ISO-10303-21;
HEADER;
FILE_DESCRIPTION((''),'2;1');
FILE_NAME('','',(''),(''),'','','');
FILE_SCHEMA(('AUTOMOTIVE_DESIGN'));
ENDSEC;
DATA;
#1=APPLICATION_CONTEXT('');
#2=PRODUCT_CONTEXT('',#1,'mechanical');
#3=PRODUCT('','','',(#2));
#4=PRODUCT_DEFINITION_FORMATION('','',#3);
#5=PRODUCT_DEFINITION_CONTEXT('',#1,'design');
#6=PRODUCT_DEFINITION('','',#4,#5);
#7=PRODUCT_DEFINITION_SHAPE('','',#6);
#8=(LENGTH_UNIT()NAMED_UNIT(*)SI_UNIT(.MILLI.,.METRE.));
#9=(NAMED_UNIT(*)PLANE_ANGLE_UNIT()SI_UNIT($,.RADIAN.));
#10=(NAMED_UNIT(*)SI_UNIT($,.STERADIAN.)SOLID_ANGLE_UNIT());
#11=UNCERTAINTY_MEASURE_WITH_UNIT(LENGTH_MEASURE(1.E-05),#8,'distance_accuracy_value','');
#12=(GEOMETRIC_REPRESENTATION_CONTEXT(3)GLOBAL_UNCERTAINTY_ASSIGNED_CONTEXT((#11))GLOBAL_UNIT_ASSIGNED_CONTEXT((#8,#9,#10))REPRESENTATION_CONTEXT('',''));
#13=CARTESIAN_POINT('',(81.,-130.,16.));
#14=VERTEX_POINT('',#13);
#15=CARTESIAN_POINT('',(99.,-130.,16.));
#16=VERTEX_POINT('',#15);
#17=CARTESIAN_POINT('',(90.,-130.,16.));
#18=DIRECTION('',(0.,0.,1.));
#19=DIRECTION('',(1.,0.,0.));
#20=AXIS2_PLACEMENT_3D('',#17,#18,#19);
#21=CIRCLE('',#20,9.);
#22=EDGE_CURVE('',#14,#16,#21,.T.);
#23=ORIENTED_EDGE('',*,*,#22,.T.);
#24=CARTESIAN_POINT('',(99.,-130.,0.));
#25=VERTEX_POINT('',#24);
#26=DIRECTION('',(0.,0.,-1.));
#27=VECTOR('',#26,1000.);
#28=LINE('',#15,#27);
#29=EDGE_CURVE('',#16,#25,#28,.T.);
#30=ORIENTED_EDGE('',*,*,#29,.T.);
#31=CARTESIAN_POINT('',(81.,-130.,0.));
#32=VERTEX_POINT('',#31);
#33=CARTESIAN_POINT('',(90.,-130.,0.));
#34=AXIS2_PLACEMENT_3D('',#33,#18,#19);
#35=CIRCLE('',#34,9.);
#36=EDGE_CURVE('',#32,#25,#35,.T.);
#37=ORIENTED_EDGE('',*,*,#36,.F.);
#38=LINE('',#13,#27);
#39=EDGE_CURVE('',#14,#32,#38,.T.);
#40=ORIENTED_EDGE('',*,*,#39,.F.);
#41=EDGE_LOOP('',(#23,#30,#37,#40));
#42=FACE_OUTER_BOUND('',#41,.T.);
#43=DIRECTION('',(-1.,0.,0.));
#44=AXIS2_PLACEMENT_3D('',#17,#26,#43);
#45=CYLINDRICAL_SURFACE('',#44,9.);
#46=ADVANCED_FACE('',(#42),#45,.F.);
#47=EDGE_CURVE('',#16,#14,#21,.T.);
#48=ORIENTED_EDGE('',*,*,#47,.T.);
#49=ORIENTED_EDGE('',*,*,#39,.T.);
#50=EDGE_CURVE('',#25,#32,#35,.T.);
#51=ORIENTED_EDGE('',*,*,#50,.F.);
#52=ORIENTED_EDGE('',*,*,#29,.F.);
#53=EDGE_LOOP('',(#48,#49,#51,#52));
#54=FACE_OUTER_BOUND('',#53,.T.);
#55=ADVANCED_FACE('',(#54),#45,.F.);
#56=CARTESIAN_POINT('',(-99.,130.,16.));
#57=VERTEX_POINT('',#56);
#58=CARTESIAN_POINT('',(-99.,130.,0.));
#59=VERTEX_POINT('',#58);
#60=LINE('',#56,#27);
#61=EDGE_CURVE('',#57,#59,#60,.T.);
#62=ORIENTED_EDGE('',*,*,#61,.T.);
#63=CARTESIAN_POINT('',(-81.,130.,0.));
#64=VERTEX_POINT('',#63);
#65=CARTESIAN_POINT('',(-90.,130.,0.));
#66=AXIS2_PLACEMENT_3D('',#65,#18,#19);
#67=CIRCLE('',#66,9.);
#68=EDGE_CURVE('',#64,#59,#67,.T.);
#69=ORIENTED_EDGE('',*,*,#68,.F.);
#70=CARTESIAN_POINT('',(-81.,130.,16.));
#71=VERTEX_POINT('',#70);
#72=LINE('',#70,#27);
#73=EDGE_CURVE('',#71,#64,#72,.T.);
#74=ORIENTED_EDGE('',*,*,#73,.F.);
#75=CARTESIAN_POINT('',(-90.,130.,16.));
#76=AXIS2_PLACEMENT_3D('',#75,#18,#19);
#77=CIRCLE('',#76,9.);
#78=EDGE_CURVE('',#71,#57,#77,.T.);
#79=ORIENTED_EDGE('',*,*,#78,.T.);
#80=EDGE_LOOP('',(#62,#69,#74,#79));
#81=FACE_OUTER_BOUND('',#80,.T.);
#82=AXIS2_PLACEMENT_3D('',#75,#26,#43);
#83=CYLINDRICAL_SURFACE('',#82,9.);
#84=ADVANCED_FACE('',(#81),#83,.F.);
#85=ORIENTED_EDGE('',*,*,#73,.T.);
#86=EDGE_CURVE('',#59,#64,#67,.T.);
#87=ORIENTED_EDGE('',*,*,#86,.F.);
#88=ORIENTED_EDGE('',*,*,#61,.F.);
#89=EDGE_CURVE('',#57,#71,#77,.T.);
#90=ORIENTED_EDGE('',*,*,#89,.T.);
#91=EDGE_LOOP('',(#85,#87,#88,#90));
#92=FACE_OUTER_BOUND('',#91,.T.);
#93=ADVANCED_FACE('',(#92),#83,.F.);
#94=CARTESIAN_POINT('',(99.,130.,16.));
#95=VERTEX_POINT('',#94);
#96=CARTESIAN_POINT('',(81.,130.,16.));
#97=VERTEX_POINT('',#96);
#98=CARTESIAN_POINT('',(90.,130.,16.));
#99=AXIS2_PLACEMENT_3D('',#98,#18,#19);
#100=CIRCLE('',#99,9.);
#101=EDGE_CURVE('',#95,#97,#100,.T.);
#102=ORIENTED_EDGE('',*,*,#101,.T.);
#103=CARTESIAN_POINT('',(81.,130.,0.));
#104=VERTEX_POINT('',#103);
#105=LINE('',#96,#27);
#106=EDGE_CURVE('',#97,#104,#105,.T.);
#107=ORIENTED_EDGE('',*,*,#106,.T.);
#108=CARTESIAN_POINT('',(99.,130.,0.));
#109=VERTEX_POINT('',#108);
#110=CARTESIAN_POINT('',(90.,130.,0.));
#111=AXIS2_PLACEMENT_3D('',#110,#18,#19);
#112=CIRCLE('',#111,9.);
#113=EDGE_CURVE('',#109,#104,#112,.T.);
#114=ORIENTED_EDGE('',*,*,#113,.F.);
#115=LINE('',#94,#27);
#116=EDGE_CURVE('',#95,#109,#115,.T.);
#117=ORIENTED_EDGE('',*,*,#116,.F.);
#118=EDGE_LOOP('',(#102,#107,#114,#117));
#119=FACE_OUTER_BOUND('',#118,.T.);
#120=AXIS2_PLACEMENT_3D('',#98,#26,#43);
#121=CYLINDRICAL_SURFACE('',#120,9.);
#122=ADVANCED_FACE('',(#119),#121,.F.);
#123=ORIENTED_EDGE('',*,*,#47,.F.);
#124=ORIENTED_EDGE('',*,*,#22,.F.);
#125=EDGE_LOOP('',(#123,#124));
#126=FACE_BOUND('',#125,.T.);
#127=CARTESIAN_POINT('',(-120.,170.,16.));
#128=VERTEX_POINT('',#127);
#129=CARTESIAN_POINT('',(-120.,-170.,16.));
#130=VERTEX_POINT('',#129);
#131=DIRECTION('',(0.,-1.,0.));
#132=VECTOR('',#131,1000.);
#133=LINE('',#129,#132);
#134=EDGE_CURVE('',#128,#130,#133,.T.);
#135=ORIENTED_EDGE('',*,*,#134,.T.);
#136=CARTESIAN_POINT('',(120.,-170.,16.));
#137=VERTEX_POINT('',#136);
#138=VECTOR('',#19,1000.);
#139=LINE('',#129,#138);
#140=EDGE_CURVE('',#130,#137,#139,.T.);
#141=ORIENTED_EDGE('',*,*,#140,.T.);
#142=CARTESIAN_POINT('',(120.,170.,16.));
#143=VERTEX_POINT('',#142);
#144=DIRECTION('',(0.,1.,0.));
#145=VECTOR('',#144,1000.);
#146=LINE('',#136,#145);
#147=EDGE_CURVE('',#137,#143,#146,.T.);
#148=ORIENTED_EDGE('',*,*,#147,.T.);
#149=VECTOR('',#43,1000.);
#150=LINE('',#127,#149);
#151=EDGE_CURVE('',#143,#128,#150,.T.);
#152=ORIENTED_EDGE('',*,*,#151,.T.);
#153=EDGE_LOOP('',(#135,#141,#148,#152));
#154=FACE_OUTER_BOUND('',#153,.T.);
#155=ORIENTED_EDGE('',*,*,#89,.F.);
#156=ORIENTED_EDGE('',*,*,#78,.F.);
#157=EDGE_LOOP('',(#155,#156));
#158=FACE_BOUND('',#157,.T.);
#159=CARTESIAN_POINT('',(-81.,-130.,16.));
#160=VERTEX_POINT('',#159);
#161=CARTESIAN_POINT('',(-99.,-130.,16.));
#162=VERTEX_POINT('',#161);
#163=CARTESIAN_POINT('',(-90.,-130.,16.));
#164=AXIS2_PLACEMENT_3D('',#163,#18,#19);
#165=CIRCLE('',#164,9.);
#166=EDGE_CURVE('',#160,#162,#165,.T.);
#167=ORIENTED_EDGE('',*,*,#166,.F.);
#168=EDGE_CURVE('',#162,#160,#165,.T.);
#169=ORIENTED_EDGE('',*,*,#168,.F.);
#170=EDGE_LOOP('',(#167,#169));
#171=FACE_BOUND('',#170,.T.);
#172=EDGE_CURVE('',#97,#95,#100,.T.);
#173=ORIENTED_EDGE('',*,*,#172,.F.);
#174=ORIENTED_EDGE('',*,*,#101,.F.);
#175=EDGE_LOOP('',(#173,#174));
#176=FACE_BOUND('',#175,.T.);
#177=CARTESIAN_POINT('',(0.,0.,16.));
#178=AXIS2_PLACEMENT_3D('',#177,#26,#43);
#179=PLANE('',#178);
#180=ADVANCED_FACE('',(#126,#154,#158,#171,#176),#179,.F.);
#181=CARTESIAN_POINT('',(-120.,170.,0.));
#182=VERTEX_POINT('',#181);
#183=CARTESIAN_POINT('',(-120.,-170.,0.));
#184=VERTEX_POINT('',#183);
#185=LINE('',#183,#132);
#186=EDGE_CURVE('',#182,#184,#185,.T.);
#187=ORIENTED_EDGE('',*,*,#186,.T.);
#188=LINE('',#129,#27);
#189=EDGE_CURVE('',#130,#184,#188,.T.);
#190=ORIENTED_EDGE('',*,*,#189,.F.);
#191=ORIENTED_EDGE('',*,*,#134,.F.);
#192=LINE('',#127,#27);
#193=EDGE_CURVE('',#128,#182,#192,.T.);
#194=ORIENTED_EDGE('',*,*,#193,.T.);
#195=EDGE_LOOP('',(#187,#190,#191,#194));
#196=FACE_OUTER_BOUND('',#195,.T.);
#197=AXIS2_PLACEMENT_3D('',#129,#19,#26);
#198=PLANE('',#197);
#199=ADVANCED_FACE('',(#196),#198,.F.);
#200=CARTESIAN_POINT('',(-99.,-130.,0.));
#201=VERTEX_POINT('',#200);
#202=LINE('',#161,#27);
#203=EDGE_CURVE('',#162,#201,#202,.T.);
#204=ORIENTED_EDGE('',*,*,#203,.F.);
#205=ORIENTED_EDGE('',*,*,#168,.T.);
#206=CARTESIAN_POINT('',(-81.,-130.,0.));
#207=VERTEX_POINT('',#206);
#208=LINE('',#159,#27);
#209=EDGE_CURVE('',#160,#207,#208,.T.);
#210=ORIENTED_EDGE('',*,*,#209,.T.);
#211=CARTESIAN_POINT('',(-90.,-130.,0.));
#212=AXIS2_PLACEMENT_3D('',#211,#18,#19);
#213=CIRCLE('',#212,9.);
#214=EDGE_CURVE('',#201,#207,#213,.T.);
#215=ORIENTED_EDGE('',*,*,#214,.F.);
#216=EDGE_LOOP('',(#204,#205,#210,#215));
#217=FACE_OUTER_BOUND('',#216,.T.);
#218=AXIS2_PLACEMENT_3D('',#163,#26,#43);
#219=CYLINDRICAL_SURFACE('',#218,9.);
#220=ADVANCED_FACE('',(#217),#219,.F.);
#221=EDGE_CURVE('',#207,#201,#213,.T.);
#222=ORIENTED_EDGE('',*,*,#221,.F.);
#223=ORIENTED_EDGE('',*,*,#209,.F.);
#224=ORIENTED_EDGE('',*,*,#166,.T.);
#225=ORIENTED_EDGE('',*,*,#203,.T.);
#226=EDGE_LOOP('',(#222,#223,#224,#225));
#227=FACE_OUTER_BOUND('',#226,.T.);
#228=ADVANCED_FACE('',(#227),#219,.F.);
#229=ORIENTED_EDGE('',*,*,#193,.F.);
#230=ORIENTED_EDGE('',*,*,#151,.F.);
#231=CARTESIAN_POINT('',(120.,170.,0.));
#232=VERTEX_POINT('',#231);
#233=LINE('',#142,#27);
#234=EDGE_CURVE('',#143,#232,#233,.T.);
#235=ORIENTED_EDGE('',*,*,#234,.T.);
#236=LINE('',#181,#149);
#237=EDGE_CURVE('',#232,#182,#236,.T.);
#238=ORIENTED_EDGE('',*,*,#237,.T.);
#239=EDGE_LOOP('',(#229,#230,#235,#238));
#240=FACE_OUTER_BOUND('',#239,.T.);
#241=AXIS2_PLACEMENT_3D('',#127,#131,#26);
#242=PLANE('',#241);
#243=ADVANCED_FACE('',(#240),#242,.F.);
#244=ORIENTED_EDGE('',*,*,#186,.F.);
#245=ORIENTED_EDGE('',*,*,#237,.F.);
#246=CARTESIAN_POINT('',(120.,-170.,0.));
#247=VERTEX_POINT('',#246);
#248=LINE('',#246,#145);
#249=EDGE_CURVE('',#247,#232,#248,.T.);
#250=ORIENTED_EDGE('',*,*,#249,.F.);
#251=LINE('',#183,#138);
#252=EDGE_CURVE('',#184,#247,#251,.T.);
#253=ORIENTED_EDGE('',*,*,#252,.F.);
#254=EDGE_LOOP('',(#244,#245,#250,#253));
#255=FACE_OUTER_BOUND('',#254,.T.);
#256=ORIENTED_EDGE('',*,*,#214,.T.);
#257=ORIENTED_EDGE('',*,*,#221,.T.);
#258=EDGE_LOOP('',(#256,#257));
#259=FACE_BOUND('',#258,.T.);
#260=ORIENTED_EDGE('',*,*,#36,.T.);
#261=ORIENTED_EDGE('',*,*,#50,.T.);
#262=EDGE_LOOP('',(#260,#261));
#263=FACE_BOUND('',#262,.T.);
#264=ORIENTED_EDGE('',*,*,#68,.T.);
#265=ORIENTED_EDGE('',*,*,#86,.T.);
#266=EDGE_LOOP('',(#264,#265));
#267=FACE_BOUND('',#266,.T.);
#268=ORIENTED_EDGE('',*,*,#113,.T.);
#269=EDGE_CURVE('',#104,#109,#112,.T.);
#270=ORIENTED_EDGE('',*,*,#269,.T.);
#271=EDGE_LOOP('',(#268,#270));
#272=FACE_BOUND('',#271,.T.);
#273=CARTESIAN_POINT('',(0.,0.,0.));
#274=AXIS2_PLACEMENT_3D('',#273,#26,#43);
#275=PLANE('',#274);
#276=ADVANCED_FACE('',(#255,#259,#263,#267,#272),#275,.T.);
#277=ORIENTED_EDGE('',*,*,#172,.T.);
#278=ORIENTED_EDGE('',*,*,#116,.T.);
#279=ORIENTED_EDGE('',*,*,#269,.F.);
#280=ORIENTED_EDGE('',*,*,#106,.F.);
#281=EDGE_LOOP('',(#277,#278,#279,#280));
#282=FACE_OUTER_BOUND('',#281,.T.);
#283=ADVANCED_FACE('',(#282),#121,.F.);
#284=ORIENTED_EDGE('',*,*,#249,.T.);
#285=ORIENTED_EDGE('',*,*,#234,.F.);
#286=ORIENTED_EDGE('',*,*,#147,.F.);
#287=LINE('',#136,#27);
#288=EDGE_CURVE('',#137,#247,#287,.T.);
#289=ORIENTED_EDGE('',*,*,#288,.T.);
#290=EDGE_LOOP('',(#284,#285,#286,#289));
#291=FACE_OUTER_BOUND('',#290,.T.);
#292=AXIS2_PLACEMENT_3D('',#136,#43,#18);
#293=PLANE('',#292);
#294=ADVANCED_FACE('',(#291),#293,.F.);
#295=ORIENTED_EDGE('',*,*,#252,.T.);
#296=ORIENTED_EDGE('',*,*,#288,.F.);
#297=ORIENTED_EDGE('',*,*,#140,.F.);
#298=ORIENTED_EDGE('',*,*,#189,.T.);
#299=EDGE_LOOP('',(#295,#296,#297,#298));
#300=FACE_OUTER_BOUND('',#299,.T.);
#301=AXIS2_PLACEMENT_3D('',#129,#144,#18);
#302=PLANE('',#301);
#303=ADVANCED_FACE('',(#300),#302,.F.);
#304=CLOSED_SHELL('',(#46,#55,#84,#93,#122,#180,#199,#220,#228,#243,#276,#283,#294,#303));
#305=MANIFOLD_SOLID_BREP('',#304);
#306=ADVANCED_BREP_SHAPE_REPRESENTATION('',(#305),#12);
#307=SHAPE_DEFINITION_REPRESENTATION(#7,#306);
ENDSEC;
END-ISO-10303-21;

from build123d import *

# Parameters (mm, degrees)
SKETCH2_W           = 240
SKETCH2_H           = 340
SKETCH2_R           = 9
BOSS_EXTRUDE1_DEPTH = 16


with BuildPart() as part:
    # Sketch2 → Boss-Extrude1 (new body)
    with BuildSketch(Plane.XY):
        Rectangle(SKETCH2_W, SKETCH2_H)
        with Locations((-90, 130)):
            Circle(SKETCH2_R, mode=Mode.SUBTRACT)
        with Locations((90, 130)):
            Circle(SKETCH2_R, mode=Mode.SUBTRACT)
        with Locations((90, -130)):
            Circle(SKETCH2_R, mode=Mode.SUBTRACT)
        with Locations((-90, -130)):
            Circle(SKETCH2_R, mode=Mode.SUBTRACT)
    extrude(amount=BOSS_EXTRUDE1_DEPTH)


solid = part.part
